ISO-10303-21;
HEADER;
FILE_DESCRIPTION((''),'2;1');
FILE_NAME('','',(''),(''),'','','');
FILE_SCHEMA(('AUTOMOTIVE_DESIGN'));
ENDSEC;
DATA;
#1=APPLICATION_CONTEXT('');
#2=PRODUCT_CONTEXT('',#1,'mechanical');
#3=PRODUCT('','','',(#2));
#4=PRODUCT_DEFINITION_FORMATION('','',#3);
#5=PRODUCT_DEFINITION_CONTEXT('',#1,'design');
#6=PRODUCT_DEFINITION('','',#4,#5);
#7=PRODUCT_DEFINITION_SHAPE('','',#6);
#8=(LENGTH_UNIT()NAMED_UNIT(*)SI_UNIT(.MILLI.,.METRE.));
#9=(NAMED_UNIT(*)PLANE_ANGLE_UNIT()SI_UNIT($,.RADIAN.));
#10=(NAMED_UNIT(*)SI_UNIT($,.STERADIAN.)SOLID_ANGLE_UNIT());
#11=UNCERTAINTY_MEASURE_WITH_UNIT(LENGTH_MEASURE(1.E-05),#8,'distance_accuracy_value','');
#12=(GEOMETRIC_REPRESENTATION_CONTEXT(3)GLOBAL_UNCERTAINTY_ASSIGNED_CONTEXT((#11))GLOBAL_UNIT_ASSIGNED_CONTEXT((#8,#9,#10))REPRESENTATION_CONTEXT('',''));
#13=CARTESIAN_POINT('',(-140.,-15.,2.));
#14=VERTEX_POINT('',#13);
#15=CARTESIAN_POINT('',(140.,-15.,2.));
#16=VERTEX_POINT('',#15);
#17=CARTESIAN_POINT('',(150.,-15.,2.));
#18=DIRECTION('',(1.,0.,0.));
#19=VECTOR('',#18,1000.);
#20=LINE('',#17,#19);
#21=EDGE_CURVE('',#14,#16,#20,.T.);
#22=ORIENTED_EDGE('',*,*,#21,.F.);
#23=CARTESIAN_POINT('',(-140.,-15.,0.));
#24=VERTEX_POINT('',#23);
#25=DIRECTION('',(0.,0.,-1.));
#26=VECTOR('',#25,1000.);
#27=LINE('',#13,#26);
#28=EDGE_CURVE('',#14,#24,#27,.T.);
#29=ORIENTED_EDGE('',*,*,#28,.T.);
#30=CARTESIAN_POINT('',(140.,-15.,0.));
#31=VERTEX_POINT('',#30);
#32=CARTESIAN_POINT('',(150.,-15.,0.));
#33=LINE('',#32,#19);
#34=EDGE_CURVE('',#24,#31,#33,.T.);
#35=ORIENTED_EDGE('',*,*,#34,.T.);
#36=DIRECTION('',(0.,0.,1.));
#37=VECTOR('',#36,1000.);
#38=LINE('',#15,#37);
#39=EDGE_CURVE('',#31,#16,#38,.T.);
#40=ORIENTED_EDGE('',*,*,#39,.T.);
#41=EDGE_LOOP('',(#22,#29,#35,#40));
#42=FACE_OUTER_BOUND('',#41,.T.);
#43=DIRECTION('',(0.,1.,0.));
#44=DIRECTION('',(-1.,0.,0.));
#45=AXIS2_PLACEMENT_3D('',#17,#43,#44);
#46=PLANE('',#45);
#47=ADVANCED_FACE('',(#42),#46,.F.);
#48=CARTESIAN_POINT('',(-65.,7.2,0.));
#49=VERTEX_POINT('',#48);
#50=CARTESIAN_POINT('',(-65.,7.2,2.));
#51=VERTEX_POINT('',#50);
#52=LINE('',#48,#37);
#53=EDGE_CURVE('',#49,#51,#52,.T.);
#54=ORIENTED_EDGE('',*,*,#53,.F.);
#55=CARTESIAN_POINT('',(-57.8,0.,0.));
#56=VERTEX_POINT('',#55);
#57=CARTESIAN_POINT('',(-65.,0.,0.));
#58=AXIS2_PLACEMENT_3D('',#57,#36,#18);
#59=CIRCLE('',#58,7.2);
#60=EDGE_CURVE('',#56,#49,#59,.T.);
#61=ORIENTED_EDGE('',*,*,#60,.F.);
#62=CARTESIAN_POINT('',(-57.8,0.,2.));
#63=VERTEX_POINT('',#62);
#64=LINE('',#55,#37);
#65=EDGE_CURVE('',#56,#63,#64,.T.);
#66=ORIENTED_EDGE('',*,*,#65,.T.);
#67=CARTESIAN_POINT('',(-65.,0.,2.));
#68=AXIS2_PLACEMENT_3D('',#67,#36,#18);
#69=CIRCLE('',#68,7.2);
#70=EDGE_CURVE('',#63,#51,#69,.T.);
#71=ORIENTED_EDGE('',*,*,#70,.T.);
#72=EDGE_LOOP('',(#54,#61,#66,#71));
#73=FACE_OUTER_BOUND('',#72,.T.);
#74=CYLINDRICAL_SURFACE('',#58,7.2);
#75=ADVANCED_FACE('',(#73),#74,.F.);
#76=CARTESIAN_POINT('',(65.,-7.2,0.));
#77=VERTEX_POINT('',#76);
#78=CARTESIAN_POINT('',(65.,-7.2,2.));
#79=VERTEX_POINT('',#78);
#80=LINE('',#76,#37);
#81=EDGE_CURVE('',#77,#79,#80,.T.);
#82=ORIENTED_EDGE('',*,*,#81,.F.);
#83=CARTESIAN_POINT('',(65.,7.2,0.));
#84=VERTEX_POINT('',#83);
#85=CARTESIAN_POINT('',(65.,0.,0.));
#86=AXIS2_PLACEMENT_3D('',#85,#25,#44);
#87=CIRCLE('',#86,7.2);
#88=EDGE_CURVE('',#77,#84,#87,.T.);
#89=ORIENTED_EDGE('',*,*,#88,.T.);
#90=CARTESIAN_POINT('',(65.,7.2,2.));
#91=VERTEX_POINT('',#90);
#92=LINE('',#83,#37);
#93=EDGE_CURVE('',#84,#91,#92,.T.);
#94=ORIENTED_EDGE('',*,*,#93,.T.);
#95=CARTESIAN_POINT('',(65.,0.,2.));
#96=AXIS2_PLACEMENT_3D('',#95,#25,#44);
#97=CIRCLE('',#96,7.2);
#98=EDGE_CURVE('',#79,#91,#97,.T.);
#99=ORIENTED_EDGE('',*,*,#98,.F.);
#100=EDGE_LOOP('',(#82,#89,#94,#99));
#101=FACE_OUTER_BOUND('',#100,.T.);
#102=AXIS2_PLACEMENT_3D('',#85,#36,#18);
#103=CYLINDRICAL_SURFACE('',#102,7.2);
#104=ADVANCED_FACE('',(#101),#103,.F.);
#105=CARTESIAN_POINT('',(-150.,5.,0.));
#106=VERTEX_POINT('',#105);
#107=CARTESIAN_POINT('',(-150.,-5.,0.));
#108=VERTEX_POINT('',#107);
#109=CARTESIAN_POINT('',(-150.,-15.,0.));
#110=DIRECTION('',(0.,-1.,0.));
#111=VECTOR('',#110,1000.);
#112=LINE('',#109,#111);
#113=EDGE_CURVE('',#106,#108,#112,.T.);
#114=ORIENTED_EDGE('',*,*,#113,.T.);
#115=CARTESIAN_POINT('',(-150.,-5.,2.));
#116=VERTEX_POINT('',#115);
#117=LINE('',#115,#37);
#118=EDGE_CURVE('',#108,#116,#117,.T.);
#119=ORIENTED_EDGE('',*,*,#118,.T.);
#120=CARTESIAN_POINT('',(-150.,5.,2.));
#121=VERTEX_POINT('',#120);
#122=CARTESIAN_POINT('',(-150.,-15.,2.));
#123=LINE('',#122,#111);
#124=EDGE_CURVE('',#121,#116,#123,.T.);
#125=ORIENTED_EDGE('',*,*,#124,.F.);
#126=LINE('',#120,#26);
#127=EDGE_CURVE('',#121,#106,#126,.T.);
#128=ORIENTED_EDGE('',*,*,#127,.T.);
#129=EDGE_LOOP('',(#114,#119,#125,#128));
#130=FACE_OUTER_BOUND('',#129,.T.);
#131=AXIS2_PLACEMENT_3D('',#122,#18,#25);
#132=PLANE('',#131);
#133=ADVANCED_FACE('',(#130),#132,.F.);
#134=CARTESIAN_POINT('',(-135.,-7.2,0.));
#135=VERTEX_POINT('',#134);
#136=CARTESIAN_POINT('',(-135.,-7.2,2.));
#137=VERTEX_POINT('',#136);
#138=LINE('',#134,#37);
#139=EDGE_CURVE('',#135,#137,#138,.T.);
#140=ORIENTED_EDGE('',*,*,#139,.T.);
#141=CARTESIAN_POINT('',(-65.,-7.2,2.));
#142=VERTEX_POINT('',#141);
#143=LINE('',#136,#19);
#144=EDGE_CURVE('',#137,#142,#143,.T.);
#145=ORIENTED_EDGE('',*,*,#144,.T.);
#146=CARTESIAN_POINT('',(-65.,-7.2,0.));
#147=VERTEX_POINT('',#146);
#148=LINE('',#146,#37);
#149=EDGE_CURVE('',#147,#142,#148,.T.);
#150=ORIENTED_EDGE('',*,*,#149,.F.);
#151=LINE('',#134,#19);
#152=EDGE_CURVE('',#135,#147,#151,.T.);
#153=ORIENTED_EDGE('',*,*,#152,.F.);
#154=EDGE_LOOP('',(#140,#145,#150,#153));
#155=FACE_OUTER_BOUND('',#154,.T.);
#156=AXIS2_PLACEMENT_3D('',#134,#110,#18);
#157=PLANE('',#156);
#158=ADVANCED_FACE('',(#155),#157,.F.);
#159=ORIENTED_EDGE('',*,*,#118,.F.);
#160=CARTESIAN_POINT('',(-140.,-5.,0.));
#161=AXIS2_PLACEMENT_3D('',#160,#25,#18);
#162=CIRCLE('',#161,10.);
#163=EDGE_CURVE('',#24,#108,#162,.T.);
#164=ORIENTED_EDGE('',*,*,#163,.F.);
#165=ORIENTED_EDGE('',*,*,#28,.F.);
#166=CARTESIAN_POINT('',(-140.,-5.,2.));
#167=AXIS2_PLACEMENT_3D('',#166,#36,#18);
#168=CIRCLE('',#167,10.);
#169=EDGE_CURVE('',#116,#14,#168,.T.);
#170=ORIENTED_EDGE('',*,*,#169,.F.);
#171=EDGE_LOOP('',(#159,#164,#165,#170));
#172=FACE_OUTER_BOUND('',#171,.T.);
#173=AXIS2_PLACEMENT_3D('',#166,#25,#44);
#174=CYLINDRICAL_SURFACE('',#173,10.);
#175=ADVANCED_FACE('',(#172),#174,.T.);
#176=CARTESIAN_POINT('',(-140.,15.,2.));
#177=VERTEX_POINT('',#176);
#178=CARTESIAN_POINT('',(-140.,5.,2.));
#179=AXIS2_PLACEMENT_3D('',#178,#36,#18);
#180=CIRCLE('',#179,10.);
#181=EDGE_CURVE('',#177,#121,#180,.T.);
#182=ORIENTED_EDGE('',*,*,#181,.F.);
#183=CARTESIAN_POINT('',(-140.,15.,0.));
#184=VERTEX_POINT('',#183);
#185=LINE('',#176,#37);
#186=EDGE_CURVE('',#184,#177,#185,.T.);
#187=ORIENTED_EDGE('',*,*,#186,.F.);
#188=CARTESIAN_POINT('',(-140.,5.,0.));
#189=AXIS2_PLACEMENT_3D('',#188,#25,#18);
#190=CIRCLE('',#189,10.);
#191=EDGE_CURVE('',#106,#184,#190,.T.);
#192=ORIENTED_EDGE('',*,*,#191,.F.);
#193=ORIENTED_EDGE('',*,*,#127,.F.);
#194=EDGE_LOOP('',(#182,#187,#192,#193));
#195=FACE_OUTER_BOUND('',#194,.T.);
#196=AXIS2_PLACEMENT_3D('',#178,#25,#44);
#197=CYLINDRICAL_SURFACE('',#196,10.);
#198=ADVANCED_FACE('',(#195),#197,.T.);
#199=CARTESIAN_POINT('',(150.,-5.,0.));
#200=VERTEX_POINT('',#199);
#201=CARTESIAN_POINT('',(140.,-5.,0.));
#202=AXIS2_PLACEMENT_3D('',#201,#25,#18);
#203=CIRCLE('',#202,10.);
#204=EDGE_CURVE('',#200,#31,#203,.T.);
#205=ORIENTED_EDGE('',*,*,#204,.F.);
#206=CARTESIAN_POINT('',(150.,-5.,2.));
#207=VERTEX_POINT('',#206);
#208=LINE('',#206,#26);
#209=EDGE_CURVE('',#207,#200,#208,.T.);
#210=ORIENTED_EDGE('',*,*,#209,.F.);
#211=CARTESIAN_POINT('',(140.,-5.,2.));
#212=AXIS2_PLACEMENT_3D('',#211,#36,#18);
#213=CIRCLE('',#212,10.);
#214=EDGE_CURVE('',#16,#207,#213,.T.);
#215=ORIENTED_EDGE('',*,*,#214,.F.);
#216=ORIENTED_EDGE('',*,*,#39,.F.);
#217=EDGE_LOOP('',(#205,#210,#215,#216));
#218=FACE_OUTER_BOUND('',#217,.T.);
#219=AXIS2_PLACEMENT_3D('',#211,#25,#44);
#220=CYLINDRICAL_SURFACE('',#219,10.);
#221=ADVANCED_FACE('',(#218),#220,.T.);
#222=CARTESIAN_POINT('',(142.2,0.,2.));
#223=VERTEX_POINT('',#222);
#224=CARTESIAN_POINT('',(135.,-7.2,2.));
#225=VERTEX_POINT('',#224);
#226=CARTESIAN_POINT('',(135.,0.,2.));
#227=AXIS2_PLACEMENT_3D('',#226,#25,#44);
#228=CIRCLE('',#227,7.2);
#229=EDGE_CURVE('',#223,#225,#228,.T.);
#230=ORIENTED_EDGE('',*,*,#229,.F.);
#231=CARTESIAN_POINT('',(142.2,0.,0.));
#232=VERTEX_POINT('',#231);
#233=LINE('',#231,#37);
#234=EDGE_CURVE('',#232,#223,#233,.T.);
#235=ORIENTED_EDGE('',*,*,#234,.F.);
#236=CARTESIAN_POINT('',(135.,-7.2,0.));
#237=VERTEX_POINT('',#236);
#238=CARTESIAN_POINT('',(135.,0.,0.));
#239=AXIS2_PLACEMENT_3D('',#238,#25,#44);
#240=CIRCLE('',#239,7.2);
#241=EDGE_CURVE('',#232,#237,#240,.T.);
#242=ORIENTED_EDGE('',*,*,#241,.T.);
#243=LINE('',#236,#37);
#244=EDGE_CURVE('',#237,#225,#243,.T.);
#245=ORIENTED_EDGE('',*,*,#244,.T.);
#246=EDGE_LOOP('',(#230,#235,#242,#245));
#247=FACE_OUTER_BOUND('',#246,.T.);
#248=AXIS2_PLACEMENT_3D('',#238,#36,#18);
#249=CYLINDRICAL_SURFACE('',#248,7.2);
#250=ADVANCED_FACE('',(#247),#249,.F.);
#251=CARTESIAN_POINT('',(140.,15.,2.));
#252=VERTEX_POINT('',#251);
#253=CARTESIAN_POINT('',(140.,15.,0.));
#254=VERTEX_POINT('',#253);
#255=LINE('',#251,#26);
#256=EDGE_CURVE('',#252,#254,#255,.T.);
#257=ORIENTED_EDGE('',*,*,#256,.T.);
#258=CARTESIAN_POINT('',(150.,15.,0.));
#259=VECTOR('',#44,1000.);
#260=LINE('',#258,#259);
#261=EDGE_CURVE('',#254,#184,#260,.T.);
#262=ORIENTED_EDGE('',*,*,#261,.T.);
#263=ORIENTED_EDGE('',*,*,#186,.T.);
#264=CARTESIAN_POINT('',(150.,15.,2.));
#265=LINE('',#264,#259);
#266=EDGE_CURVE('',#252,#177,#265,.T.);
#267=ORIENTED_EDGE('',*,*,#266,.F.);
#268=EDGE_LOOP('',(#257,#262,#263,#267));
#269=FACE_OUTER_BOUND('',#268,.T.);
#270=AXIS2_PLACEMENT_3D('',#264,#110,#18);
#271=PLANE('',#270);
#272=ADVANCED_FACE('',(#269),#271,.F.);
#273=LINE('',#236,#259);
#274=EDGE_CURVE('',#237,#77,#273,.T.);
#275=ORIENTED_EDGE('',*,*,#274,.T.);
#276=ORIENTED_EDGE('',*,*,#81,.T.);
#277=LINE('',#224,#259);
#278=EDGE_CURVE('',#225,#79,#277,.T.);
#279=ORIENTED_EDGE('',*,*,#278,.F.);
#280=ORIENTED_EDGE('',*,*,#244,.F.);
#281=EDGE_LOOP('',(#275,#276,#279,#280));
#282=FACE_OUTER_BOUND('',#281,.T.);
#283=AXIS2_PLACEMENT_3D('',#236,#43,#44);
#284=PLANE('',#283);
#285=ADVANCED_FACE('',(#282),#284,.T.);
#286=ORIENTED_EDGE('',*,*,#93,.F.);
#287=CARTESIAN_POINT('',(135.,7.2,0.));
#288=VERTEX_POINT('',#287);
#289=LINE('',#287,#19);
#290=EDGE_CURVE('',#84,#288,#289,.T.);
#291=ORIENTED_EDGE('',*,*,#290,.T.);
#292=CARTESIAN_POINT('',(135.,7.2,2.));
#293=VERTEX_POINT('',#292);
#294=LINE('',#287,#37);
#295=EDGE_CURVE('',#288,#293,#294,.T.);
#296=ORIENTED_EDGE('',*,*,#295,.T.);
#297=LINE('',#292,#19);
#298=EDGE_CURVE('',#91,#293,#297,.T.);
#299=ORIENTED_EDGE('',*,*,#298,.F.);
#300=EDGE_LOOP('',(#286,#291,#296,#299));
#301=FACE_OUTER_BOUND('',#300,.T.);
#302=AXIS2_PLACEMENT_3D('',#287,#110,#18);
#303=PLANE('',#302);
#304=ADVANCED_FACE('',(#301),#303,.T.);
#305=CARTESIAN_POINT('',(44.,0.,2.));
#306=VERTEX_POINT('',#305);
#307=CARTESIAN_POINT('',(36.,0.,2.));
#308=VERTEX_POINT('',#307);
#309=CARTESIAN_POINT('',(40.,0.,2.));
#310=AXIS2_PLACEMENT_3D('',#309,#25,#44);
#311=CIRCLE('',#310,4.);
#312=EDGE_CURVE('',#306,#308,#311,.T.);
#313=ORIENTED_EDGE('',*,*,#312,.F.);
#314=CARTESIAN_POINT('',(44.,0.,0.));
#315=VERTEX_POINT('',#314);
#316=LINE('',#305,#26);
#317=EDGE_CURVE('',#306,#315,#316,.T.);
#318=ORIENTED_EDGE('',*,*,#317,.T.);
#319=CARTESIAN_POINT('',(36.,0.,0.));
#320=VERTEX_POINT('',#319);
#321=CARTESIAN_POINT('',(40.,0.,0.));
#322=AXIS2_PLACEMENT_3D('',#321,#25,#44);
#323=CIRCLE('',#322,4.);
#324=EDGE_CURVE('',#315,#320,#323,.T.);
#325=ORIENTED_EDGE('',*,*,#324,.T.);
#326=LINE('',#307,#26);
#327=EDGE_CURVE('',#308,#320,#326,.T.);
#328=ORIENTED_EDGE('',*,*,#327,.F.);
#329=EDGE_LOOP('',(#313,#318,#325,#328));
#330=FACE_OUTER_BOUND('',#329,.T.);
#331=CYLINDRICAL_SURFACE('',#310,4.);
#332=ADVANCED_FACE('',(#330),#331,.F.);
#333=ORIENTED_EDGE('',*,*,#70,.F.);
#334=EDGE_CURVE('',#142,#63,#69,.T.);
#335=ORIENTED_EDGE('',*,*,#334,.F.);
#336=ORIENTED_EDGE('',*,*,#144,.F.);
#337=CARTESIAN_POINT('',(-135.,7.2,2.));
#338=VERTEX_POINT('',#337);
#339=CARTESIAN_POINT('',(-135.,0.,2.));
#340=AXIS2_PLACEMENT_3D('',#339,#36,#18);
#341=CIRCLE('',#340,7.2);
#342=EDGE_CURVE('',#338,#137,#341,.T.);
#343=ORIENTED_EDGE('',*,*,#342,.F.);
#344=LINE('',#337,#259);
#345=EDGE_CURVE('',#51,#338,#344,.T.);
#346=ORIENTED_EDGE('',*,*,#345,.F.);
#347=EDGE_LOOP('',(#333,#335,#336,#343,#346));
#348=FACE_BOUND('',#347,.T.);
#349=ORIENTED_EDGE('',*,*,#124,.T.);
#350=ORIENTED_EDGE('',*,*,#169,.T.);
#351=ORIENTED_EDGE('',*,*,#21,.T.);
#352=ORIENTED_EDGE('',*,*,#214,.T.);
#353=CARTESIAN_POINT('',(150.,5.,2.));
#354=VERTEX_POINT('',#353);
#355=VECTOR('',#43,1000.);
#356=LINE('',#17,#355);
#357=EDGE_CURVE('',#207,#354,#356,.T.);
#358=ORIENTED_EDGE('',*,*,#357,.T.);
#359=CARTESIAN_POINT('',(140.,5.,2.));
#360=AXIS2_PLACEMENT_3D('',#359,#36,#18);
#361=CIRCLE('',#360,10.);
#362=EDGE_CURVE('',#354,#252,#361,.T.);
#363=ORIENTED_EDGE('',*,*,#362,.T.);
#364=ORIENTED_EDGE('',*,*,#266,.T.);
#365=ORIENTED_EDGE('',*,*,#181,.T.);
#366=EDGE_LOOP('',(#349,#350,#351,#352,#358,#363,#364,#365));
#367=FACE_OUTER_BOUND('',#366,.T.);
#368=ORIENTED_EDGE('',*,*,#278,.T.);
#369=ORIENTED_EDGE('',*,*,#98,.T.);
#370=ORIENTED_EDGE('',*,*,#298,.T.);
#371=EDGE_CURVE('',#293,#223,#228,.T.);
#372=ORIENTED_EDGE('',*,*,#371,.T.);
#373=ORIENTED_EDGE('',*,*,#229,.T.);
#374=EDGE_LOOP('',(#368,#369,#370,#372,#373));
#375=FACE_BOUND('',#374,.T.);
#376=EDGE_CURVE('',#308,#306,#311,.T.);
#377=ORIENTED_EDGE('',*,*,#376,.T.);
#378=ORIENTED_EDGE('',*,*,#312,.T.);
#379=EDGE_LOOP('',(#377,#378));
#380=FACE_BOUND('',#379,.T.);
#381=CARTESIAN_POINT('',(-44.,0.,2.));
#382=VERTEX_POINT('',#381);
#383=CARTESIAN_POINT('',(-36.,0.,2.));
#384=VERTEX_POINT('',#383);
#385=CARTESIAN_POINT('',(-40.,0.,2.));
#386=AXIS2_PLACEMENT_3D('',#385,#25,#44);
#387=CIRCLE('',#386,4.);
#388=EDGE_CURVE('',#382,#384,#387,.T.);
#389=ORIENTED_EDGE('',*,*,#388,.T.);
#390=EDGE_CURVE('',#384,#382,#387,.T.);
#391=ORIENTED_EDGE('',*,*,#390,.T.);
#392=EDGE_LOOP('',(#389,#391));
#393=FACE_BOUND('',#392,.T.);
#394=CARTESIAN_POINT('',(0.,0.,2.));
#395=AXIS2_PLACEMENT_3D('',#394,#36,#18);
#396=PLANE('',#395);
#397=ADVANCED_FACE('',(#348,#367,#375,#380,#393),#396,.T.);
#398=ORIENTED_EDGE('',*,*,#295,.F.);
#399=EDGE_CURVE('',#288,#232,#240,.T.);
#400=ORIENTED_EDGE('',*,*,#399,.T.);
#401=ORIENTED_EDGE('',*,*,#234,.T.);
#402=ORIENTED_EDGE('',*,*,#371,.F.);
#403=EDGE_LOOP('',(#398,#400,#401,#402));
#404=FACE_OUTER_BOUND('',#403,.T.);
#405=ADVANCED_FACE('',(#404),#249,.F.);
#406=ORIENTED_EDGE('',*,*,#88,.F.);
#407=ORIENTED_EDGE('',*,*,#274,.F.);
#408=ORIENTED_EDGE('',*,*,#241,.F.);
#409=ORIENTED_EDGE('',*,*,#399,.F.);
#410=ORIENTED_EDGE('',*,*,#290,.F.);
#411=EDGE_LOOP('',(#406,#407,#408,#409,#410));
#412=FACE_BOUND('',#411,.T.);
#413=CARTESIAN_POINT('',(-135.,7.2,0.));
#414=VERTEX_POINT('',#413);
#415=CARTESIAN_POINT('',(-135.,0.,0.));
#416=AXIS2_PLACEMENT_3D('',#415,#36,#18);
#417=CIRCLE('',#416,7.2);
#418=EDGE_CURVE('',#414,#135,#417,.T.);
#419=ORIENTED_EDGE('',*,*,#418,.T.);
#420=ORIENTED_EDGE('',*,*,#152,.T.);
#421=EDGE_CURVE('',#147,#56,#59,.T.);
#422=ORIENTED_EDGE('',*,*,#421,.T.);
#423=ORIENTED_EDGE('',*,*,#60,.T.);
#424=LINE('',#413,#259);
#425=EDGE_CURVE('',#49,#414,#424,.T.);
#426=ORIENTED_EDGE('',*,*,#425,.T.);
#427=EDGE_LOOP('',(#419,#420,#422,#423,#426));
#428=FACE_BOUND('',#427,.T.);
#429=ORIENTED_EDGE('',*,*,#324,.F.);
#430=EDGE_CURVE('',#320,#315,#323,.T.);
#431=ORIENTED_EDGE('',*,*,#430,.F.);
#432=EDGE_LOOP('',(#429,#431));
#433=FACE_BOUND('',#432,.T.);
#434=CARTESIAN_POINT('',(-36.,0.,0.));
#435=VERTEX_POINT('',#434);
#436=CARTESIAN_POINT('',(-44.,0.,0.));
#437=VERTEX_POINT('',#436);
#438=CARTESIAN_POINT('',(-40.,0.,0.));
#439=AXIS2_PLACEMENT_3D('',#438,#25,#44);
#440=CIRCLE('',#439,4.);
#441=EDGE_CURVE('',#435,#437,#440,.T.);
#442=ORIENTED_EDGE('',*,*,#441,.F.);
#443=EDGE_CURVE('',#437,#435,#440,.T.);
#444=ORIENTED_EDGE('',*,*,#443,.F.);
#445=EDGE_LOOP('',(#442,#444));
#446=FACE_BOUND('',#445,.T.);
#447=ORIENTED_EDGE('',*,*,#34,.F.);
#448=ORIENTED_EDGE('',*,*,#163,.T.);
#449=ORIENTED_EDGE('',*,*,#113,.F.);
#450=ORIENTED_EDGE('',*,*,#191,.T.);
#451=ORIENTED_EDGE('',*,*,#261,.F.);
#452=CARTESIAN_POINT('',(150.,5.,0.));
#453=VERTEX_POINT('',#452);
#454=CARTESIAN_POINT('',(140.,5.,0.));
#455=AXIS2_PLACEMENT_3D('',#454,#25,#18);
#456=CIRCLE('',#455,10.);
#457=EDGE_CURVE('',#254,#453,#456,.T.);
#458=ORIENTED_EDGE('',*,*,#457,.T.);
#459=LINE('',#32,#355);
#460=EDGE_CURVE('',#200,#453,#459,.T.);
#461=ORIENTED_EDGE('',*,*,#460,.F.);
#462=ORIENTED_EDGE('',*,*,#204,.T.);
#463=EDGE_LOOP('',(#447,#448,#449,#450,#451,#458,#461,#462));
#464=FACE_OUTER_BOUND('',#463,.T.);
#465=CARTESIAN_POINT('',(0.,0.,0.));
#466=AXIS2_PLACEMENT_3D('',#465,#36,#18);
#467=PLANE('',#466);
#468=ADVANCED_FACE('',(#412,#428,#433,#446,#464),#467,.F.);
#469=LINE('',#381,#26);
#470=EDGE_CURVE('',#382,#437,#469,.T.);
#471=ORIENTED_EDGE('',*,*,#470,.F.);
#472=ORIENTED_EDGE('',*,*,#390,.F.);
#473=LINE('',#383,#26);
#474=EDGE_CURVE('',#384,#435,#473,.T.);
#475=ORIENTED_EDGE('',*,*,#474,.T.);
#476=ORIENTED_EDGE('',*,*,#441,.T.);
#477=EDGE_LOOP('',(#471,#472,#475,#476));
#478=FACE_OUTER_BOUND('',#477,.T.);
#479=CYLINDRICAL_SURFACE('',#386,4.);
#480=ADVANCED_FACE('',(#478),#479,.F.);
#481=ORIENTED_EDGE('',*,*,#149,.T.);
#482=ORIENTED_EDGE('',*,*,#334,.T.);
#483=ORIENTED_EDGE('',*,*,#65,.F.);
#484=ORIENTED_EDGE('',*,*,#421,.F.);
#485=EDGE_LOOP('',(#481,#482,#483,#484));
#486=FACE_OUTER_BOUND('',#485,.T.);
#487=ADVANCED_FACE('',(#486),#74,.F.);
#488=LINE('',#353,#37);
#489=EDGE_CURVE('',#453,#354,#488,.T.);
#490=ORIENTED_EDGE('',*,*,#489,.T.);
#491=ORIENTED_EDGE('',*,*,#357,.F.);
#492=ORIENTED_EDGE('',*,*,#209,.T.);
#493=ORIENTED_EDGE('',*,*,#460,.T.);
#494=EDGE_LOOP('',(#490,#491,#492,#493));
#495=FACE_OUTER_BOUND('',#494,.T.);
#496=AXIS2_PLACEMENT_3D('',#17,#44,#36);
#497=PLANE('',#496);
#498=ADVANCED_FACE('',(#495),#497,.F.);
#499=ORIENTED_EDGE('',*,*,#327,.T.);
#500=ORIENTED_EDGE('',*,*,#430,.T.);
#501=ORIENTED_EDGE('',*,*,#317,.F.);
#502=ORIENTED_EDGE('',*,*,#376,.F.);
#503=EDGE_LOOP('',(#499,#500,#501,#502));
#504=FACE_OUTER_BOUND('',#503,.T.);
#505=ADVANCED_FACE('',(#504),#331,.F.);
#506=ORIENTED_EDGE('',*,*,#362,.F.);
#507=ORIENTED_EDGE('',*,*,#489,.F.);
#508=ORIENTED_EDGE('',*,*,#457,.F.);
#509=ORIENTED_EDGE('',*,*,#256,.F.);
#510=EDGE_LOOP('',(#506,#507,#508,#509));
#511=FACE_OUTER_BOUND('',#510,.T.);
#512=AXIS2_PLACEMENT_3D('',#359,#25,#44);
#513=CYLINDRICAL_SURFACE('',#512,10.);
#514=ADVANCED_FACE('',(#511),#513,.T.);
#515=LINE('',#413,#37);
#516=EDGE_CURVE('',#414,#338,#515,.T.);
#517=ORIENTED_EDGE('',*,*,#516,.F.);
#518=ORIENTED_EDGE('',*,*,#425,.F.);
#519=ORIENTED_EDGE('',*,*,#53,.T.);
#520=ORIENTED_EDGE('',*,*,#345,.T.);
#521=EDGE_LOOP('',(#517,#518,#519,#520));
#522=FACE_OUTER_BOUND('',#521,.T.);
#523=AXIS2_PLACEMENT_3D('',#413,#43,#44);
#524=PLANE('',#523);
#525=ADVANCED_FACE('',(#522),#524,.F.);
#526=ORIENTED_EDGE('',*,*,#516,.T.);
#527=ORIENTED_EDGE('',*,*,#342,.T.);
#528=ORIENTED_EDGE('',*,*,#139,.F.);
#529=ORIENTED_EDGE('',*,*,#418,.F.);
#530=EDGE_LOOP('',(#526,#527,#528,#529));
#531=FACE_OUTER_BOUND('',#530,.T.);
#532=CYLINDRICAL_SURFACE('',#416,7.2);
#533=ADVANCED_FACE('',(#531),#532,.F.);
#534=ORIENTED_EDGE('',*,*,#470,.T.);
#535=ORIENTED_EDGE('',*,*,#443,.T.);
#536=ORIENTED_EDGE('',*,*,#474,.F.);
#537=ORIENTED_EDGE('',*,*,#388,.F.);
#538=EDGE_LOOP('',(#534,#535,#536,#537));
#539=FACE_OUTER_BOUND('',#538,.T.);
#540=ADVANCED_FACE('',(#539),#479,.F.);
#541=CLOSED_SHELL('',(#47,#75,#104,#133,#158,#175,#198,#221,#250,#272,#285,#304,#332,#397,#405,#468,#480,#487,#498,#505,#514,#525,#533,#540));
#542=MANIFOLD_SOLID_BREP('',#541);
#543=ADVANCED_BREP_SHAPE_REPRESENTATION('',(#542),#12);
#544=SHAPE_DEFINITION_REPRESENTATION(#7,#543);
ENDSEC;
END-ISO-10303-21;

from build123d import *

# Parameters (mm, degrees)
SKETCH1_W           = 300
SKETCH1_H           = 30
BOSS_EXTRUDE1_DEPTH = 2
CUT_EXTRUDE1_DEPTH  = 151.761400896
FILLET1_R           = 10
FILLET2_R           = 10
SKETCH4_R           = 4
CUT_EXTRUDE2_DEPTH  = 151.761400896


with BuildPart() as part:
    # Sketch1 → Boss-Extrude1 (new body)
    with BuildSketch(Plane.XY):
        Rectangle(SKETCH1_W, SKETCH1_H)
    extrude(amount=BOSS_EXTRUDE1_DEPTH)

    # Sketch2 → Cut-Extrude1 (cut, through all)
    with BuildSketch(Plane.XY.offset(2)):
        with BuildLine():
            Line((-135, 7.2), (-65, 7.2))
            ThreePointArc((-65, 7.2), (-57.8, 0), (-65, -7.2))
            Line((-65, -7.2), (-135, -7.2))
            ThreePointArc((-135, -7.2), (-142.2, 0), (-135, 7.2))
        make_face()
    cut_extrude1 = extrude(amount=-CUT_EXTRUDE1_DEPTH, mode=Mode.SUBTRACT)

    # Fillet1
    fillet1_edges = [part.edges().sort_by_distance(p)[0] for p in [
        (-150, 15, 1),
        (-150, -15, 1),
    ]]
    fillet(fillet1_edges, radius=FILLET1_R)

    # Mirror1: Cut-Extrude1 across plane
    add(cut_extrude1.mirror(Plane(origin=(0, 0, 0), x_dir=(0, 0, 1), z_dir=(1, 0, 0))), mode=Mode.SUBTRACT)

    # Fillet2
    fillet2_edges = [part.edges().sort_by_distance(p)[0] for p in [
        (150, 15, 1),
        (150, -15, 1),
    ]]
    fillet(fillet2_edges, radius=FILLET2_R)

    # Sketch4 → Cut-Extrude2 (cut, through all)
    with BuildSketch(Plane(origin=(0, 0, 0), x_dir=(-1, 0, 0), z_dir=(0, 0, -1))):
        with Locations((40, 0)):
            Circle(SKETCH4_R)
        with Locations((-40, 0)):
            Circle(SKETCH4_R)
    extrude(amount=-CUT_EXTRUDE2_DEPTH, mode=Mode.SUBTRACT)


solid = part.part
